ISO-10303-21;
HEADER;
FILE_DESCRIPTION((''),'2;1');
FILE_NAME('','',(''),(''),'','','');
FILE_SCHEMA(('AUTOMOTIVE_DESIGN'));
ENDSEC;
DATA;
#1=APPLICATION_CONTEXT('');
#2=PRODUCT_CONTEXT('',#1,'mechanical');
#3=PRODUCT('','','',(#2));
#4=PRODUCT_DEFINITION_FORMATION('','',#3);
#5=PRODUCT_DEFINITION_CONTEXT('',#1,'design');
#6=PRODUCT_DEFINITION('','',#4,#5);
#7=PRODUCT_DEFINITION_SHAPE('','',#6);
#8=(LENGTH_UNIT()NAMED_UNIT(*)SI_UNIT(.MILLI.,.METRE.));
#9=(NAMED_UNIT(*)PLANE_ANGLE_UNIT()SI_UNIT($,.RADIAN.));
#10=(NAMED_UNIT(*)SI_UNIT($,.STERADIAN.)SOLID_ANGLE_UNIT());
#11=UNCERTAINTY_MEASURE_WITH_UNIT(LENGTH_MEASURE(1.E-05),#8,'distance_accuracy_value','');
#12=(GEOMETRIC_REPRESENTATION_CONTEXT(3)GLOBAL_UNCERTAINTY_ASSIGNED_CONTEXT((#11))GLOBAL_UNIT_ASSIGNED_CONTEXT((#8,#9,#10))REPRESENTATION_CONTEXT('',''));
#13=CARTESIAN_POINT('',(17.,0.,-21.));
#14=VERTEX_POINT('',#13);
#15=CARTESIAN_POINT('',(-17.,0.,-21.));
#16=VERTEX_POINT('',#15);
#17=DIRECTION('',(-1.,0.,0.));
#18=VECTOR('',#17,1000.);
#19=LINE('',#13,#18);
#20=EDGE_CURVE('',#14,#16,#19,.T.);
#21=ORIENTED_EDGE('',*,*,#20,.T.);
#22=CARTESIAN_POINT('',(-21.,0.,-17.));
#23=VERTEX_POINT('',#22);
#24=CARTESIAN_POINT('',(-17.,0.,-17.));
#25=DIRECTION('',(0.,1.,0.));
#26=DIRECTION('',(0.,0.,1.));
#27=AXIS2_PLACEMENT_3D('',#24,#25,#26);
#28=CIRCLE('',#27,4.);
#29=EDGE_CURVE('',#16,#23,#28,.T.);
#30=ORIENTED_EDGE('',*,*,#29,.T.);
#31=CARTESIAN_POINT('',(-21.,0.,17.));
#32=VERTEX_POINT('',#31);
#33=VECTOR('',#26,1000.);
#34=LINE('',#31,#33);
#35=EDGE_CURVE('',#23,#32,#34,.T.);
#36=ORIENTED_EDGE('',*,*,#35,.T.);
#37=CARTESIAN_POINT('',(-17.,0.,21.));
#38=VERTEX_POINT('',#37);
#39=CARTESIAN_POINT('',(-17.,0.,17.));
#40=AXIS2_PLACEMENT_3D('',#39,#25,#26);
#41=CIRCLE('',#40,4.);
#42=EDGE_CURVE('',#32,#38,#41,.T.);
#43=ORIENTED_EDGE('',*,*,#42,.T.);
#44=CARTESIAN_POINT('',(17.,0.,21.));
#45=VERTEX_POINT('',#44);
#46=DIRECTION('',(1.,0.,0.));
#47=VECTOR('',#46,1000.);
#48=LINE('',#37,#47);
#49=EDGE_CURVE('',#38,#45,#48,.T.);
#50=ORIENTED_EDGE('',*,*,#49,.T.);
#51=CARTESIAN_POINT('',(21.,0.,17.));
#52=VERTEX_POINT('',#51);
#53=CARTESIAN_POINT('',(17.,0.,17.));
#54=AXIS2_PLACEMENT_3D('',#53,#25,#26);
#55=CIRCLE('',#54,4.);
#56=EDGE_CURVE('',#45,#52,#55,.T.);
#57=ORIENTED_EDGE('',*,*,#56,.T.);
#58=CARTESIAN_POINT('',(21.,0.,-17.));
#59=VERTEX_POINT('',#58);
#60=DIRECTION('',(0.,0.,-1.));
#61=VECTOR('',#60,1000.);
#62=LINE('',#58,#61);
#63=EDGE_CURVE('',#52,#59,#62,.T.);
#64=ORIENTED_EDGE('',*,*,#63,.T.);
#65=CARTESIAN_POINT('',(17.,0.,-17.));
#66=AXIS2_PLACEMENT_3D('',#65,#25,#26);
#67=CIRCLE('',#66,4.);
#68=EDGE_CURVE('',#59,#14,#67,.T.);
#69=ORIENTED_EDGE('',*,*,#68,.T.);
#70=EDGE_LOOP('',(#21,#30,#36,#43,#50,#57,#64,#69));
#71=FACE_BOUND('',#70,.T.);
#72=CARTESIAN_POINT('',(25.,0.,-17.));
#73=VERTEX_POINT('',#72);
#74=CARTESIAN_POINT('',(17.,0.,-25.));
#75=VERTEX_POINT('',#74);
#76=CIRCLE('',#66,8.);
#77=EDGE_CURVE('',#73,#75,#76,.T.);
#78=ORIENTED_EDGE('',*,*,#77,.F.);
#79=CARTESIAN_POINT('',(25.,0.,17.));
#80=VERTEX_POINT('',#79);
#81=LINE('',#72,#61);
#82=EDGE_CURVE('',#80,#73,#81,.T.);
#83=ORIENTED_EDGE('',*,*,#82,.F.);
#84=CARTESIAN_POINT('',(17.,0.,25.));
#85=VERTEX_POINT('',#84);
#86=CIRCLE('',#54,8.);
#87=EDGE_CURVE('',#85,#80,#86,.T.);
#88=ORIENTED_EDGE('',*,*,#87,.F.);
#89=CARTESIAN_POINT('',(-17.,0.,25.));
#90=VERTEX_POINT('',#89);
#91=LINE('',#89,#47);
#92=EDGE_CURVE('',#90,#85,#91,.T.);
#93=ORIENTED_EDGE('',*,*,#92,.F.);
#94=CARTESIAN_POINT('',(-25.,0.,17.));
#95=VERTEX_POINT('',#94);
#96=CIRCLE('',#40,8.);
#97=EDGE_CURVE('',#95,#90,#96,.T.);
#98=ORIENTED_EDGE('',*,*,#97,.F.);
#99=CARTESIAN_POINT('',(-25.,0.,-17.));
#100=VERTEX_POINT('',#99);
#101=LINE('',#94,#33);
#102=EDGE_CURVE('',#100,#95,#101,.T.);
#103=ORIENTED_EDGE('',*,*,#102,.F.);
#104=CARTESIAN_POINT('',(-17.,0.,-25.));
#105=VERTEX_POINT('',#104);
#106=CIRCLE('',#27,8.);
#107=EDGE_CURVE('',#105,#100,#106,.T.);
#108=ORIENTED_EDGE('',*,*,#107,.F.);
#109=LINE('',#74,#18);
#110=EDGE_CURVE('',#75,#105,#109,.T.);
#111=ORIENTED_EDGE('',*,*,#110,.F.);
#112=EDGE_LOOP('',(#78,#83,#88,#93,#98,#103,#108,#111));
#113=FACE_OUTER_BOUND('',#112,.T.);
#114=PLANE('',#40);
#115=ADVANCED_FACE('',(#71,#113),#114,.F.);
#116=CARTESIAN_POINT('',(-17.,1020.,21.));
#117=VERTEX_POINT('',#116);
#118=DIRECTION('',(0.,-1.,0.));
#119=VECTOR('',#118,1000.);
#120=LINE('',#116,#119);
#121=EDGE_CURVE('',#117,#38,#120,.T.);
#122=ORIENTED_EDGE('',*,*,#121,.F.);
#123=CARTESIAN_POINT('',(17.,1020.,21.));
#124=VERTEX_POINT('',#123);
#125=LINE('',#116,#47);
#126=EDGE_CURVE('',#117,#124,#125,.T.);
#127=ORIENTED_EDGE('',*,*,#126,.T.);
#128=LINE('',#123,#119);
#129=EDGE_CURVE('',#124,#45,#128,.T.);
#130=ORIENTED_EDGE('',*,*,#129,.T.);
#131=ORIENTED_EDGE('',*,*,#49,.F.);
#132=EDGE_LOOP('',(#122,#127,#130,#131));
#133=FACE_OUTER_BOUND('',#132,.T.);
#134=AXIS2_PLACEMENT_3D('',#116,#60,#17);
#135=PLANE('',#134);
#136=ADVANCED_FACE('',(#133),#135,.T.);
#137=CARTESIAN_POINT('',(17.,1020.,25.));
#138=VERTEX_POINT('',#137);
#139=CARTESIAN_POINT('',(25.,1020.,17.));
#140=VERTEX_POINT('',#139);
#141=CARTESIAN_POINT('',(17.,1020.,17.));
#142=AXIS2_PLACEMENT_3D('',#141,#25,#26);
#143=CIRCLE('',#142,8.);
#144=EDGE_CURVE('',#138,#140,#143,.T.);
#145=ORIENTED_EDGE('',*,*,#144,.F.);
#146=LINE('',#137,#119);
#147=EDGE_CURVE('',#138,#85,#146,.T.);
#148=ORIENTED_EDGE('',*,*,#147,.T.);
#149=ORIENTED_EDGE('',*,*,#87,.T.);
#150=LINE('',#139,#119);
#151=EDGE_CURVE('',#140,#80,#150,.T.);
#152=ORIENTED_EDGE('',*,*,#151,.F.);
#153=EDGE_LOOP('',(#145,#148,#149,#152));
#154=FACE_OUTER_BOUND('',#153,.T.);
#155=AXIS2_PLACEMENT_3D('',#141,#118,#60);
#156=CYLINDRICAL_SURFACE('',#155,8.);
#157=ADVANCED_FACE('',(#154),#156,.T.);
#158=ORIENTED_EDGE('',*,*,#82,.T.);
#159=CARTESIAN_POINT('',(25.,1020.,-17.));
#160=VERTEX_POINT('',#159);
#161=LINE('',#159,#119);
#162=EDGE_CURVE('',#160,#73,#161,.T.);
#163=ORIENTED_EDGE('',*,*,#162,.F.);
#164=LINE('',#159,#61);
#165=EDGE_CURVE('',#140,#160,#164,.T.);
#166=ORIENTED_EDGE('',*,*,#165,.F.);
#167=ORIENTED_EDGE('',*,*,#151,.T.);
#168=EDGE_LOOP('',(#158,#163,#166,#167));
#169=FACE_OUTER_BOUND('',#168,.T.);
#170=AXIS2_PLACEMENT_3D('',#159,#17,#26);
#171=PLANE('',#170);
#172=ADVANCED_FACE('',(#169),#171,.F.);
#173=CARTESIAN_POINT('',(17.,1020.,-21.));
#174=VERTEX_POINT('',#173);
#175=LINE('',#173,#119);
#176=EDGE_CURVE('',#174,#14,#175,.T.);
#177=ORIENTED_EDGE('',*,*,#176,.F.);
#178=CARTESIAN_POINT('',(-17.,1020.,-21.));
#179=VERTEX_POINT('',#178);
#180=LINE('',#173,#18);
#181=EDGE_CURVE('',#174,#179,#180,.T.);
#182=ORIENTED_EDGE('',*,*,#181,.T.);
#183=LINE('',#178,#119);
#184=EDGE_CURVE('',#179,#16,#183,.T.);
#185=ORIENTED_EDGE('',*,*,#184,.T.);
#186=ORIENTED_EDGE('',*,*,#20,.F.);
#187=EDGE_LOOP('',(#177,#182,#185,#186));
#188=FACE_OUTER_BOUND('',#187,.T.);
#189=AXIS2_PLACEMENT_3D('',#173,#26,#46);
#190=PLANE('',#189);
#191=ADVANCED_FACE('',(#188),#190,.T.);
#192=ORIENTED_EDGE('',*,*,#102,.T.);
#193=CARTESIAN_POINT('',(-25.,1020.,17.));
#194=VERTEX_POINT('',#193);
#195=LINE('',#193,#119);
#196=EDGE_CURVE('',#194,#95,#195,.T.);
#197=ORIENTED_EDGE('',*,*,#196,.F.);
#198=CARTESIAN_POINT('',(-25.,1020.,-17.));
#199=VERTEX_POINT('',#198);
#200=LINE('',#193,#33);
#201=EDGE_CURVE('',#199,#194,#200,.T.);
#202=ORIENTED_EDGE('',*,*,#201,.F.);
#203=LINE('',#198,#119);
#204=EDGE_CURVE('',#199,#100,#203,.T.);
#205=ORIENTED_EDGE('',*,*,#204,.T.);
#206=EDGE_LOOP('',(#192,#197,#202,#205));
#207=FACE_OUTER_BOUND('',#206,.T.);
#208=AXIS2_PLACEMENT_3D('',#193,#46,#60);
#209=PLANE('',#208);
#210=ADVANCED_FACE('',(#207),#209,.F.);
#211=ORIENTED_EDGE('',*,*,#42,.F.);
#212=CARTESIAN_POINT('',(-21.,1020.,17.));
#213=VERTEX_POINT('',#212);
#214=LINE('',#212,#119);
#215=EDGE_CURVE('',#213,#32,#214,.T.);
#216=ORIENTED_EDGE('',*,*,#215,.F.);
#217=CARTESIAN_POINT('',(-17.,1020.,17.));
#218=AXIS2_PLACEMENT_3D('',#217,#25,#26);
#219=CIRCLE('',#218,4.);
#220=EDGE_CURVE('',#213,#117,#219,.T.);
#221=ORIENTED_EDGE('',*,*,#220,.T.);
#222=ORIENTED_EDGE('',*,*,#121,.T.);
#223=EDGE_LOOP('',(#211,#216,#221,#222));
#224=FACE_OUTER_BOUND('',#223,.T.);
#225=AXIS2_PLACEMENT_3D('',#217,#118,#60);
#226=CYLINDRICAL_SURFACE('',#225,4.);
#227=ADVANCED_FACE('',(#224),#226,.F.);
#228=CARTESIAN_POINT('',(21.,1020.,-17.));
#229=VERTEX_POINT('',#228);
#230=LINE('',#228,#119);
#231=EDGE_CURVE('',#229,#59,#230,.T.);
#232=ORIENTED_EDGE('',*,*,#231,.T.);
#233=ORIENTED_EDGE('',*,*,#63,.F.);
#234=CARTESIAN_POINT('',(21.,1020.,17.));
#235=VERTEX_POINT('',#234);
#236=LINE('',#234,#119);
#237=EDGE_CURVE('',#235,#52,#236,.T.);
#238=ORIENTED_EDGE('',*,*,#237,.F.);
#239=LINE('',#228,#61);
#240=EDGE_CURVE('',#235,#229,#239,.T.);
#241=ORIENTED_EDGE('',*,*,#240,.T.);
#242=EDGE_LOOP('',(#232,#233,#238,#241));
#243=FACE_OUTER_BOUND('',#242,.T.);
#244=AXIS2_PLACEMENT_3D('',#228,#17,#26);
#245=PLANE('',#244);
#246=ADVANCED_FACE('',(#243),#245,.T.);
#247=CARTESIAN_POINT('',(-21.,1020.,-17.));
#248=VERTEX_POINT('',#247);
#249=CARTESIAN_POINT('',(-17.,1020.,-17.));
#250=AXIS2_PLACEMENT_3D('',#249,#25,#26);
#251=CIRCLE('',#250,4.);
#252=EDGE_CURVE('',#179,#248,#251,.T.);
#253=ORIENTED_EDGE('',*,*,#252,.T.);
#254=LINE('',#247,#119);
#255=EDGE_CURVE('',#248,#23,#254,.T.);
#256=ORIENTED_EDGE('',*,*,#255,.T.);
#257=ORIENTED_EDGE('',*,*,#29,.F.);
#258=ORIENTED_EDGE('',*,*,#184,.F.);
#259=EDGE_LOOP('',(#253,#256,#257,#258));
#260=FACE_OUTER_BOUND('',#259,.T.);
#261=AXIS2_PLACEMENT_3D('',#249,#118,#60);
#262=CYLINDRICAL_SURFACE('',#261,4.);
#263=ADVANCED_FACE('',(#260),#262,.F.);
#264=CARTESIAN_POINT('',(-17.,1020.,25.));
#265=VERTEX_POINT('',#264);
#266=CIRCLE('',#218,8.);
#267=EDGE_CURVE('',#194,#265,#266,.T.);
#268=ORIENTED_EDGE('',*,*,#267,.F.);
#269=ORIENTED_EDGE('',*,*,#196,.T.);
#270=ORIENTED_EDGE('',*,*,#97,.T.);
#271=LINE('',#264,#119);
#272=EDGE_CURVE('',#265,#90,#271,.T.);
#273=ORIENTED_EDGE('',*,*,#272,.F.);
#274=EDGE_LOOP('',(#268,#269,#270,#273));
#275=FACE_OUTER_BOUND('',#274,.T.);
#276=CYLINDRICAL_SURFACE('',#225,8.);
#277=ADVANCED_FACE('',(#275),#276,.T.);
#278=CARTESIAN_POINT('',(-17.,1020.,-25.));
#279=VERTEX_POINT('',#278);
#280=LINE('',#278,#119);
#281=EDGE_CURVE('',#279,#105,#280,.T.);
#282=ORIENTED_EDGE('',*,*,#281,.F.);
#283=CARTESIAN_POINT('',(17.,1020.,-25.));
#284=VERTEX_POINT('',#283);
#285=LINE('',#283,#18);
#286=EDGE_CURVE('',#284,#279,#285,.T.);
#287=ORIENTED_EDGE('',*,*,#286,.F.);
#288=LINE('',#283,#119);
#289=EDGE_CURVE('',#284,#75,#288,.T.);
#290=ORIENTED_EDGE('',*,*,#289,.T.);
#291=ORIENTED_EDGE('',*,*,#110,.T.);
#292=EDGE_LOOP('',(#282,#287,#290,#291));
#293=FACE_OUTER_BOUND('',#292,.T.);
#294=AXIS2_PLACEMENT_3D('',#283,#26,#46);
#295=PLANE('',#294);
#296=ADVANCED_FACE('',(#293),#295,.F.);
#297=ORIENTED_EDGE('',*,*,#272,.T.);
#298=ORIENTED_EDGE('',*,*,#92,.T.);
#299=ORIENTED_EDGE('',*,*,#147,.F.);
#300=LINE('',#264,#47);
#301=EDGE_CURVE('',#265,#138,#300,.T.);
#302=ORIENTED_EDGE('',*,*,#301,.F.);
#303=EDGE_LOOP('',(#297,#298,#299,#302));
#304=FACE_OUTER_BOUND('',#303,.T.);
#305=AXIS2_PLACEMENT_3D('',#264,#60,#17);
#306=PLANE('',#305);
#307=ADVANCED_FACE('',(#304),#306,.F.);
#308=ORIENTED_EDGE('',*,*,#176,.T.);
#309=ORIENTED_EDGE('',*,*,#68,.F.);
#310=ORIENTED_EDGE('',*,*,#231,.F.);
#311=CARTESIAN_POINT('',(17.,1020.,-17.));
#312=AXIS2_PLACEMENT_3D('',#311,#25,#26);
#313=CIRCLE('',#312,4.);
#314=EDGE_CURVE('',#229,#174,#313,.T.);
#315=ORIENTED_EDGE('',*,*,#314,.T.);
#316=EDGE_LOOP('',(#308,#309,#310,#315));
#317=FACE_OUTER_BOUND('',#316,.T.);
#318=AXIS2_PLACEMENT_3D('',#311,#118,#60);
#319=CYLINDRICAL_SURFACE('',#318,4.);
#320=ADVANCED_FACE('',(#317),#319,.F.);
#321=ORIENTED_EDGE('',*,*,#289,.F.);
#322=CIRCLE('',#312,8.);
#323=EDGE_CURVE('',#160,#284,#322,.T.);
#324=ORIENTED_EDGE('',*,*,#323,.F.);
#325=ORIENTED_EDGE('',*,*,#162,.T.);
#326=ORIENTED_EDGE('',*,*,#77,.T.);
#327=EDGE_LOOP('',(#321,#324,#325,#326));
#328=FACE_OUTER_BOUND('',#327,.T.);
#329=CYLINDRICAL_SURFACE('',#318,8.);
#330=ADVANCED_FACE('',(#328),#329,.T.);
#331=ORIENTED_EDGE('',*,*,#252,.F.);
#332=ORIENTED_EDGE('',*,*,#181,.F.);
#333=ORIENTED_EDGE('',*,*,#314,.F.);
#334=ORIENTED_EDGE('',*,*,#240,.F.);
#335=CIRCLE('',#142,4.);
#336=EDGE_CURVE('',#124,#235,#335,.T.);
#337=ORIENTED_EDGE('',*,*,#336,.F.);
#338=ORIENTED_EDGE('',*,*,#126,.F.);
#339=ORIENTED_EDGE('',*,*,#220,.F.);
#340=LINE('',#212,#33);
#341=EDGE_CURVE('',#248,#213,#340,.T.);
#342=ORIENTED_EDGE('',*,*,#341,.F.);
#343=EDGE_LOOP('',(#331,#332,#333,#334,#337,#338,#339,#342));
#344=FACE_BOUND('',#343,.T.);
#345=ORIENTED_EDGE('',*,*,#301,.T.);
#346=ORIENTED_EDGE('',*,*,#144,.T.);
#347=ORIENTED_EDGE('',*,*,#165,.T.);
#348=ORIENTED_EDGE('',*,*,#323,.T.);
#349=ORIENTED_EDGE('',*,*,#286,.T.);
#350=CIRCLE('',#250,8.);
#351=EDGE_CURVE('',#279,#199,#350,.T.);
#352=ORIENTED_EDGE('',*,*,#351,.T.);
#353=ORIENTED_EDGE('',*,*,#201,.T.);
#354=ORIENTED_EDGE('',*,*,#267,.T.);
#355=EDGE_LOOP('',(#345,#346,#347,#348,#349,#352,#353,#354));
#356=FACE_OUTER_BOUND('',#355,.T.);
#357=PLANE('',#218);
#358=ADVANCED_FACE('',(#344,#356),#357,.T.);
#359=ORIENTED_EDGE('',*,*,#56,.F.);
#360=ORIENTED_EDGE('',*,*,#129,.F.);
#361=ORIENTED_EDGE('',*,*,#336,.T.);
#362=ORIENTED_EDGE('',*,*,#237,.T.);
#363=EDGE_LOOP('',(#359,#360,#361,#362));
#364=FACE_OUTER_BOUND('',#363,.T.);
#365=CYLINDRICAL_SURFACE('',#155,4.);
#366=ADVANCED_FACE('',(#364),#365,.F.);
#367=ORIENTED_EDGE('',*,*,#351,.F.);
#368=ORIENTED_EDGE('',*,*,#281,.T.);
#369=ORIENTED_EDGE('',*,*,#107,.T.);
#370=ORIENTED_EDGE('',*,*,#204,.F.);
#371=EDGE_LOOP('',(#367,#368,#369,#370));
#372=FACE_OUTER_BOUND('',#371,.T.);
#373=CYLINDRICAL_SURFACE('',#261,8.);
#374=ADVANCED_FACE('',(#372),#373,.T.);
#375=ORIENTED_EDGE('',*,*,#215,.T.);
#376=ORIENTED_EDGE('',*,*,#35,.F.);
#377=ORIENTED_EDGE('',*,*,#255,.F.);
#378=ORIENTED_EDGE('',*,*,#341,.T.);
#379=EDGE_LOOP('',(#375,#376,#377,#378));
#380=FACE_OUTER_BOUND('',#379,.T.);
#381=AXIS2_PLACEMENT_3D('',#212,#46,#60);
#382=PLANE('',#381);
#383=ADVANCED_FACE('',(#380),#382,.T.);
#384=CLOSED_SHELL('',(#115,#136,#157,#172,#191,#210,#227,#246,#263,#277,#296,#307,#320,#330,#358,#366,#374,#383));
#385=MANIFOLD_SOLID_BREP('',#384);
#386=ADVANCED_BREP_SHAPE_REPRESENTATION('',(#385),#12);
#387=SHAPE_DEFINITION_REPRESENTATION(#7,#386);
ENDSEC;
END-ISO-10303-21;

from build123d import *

# Parameters (mm, degrees)
GB_T_6728_2002_SQUARE_HOLLOW_SECTION_50_DEPTH = 1020


with BuildPart() as part:
    # Sketch1 → Gb／t 6728—2002 square hollow section 50×50×4(1) (new body)
    with BuildSketch(Plane(origin=(0, 0, 0), x_dir=(-1, 0, 0), z_dir=(0, 1, 0))):
        with BuildLine():
            Line((-17, -25), (17, -25))
            ThreePointArc((17, -25), (22.656854249, -22.656854249), (25, -17))
            Line((25, -17), (25, 17))
            ThreePointArc((25, 17), (22.656854249, 22.656854249), (17, 25))
            Line((17, 25), (-17, 25))
            ThreePointArc((-17, 25), (-22.656854249, 22.656854249), (-25, 17))
            Line((-25, 17), (-25, -17))
            ThreePointArc((-25, -17), (-22.656854249, -22.656854249), (-17, -25))
        make_face()
        with BuildLine():
            Line((-17, -21), (17, -21))
            ThreePointArc((17, -21), (19.828427125, -19.828427125), (21, -17))
            Line((21, -17), (21, 17))
            ThreePointArc((21, 17), (19.828427125, 19.828427125), (17, 21))
            Line((17, 21), (-17, 21))
            ThreePointArc((-17, 21), (-19.828427125, 19.828427125), (-21, 17))
            Line((-21, 17), (-21, -17))
            ThreePointArc((-21, -17), (-19.828427125, -19.828427125), (-17, -21))
        make_face(mode=Mode.SUBTRACT)
    extrude(amount=GB_T_6728_2002_SQUARE_HOLLOW_SECTION_50_DEPTH)


solid = part.part
